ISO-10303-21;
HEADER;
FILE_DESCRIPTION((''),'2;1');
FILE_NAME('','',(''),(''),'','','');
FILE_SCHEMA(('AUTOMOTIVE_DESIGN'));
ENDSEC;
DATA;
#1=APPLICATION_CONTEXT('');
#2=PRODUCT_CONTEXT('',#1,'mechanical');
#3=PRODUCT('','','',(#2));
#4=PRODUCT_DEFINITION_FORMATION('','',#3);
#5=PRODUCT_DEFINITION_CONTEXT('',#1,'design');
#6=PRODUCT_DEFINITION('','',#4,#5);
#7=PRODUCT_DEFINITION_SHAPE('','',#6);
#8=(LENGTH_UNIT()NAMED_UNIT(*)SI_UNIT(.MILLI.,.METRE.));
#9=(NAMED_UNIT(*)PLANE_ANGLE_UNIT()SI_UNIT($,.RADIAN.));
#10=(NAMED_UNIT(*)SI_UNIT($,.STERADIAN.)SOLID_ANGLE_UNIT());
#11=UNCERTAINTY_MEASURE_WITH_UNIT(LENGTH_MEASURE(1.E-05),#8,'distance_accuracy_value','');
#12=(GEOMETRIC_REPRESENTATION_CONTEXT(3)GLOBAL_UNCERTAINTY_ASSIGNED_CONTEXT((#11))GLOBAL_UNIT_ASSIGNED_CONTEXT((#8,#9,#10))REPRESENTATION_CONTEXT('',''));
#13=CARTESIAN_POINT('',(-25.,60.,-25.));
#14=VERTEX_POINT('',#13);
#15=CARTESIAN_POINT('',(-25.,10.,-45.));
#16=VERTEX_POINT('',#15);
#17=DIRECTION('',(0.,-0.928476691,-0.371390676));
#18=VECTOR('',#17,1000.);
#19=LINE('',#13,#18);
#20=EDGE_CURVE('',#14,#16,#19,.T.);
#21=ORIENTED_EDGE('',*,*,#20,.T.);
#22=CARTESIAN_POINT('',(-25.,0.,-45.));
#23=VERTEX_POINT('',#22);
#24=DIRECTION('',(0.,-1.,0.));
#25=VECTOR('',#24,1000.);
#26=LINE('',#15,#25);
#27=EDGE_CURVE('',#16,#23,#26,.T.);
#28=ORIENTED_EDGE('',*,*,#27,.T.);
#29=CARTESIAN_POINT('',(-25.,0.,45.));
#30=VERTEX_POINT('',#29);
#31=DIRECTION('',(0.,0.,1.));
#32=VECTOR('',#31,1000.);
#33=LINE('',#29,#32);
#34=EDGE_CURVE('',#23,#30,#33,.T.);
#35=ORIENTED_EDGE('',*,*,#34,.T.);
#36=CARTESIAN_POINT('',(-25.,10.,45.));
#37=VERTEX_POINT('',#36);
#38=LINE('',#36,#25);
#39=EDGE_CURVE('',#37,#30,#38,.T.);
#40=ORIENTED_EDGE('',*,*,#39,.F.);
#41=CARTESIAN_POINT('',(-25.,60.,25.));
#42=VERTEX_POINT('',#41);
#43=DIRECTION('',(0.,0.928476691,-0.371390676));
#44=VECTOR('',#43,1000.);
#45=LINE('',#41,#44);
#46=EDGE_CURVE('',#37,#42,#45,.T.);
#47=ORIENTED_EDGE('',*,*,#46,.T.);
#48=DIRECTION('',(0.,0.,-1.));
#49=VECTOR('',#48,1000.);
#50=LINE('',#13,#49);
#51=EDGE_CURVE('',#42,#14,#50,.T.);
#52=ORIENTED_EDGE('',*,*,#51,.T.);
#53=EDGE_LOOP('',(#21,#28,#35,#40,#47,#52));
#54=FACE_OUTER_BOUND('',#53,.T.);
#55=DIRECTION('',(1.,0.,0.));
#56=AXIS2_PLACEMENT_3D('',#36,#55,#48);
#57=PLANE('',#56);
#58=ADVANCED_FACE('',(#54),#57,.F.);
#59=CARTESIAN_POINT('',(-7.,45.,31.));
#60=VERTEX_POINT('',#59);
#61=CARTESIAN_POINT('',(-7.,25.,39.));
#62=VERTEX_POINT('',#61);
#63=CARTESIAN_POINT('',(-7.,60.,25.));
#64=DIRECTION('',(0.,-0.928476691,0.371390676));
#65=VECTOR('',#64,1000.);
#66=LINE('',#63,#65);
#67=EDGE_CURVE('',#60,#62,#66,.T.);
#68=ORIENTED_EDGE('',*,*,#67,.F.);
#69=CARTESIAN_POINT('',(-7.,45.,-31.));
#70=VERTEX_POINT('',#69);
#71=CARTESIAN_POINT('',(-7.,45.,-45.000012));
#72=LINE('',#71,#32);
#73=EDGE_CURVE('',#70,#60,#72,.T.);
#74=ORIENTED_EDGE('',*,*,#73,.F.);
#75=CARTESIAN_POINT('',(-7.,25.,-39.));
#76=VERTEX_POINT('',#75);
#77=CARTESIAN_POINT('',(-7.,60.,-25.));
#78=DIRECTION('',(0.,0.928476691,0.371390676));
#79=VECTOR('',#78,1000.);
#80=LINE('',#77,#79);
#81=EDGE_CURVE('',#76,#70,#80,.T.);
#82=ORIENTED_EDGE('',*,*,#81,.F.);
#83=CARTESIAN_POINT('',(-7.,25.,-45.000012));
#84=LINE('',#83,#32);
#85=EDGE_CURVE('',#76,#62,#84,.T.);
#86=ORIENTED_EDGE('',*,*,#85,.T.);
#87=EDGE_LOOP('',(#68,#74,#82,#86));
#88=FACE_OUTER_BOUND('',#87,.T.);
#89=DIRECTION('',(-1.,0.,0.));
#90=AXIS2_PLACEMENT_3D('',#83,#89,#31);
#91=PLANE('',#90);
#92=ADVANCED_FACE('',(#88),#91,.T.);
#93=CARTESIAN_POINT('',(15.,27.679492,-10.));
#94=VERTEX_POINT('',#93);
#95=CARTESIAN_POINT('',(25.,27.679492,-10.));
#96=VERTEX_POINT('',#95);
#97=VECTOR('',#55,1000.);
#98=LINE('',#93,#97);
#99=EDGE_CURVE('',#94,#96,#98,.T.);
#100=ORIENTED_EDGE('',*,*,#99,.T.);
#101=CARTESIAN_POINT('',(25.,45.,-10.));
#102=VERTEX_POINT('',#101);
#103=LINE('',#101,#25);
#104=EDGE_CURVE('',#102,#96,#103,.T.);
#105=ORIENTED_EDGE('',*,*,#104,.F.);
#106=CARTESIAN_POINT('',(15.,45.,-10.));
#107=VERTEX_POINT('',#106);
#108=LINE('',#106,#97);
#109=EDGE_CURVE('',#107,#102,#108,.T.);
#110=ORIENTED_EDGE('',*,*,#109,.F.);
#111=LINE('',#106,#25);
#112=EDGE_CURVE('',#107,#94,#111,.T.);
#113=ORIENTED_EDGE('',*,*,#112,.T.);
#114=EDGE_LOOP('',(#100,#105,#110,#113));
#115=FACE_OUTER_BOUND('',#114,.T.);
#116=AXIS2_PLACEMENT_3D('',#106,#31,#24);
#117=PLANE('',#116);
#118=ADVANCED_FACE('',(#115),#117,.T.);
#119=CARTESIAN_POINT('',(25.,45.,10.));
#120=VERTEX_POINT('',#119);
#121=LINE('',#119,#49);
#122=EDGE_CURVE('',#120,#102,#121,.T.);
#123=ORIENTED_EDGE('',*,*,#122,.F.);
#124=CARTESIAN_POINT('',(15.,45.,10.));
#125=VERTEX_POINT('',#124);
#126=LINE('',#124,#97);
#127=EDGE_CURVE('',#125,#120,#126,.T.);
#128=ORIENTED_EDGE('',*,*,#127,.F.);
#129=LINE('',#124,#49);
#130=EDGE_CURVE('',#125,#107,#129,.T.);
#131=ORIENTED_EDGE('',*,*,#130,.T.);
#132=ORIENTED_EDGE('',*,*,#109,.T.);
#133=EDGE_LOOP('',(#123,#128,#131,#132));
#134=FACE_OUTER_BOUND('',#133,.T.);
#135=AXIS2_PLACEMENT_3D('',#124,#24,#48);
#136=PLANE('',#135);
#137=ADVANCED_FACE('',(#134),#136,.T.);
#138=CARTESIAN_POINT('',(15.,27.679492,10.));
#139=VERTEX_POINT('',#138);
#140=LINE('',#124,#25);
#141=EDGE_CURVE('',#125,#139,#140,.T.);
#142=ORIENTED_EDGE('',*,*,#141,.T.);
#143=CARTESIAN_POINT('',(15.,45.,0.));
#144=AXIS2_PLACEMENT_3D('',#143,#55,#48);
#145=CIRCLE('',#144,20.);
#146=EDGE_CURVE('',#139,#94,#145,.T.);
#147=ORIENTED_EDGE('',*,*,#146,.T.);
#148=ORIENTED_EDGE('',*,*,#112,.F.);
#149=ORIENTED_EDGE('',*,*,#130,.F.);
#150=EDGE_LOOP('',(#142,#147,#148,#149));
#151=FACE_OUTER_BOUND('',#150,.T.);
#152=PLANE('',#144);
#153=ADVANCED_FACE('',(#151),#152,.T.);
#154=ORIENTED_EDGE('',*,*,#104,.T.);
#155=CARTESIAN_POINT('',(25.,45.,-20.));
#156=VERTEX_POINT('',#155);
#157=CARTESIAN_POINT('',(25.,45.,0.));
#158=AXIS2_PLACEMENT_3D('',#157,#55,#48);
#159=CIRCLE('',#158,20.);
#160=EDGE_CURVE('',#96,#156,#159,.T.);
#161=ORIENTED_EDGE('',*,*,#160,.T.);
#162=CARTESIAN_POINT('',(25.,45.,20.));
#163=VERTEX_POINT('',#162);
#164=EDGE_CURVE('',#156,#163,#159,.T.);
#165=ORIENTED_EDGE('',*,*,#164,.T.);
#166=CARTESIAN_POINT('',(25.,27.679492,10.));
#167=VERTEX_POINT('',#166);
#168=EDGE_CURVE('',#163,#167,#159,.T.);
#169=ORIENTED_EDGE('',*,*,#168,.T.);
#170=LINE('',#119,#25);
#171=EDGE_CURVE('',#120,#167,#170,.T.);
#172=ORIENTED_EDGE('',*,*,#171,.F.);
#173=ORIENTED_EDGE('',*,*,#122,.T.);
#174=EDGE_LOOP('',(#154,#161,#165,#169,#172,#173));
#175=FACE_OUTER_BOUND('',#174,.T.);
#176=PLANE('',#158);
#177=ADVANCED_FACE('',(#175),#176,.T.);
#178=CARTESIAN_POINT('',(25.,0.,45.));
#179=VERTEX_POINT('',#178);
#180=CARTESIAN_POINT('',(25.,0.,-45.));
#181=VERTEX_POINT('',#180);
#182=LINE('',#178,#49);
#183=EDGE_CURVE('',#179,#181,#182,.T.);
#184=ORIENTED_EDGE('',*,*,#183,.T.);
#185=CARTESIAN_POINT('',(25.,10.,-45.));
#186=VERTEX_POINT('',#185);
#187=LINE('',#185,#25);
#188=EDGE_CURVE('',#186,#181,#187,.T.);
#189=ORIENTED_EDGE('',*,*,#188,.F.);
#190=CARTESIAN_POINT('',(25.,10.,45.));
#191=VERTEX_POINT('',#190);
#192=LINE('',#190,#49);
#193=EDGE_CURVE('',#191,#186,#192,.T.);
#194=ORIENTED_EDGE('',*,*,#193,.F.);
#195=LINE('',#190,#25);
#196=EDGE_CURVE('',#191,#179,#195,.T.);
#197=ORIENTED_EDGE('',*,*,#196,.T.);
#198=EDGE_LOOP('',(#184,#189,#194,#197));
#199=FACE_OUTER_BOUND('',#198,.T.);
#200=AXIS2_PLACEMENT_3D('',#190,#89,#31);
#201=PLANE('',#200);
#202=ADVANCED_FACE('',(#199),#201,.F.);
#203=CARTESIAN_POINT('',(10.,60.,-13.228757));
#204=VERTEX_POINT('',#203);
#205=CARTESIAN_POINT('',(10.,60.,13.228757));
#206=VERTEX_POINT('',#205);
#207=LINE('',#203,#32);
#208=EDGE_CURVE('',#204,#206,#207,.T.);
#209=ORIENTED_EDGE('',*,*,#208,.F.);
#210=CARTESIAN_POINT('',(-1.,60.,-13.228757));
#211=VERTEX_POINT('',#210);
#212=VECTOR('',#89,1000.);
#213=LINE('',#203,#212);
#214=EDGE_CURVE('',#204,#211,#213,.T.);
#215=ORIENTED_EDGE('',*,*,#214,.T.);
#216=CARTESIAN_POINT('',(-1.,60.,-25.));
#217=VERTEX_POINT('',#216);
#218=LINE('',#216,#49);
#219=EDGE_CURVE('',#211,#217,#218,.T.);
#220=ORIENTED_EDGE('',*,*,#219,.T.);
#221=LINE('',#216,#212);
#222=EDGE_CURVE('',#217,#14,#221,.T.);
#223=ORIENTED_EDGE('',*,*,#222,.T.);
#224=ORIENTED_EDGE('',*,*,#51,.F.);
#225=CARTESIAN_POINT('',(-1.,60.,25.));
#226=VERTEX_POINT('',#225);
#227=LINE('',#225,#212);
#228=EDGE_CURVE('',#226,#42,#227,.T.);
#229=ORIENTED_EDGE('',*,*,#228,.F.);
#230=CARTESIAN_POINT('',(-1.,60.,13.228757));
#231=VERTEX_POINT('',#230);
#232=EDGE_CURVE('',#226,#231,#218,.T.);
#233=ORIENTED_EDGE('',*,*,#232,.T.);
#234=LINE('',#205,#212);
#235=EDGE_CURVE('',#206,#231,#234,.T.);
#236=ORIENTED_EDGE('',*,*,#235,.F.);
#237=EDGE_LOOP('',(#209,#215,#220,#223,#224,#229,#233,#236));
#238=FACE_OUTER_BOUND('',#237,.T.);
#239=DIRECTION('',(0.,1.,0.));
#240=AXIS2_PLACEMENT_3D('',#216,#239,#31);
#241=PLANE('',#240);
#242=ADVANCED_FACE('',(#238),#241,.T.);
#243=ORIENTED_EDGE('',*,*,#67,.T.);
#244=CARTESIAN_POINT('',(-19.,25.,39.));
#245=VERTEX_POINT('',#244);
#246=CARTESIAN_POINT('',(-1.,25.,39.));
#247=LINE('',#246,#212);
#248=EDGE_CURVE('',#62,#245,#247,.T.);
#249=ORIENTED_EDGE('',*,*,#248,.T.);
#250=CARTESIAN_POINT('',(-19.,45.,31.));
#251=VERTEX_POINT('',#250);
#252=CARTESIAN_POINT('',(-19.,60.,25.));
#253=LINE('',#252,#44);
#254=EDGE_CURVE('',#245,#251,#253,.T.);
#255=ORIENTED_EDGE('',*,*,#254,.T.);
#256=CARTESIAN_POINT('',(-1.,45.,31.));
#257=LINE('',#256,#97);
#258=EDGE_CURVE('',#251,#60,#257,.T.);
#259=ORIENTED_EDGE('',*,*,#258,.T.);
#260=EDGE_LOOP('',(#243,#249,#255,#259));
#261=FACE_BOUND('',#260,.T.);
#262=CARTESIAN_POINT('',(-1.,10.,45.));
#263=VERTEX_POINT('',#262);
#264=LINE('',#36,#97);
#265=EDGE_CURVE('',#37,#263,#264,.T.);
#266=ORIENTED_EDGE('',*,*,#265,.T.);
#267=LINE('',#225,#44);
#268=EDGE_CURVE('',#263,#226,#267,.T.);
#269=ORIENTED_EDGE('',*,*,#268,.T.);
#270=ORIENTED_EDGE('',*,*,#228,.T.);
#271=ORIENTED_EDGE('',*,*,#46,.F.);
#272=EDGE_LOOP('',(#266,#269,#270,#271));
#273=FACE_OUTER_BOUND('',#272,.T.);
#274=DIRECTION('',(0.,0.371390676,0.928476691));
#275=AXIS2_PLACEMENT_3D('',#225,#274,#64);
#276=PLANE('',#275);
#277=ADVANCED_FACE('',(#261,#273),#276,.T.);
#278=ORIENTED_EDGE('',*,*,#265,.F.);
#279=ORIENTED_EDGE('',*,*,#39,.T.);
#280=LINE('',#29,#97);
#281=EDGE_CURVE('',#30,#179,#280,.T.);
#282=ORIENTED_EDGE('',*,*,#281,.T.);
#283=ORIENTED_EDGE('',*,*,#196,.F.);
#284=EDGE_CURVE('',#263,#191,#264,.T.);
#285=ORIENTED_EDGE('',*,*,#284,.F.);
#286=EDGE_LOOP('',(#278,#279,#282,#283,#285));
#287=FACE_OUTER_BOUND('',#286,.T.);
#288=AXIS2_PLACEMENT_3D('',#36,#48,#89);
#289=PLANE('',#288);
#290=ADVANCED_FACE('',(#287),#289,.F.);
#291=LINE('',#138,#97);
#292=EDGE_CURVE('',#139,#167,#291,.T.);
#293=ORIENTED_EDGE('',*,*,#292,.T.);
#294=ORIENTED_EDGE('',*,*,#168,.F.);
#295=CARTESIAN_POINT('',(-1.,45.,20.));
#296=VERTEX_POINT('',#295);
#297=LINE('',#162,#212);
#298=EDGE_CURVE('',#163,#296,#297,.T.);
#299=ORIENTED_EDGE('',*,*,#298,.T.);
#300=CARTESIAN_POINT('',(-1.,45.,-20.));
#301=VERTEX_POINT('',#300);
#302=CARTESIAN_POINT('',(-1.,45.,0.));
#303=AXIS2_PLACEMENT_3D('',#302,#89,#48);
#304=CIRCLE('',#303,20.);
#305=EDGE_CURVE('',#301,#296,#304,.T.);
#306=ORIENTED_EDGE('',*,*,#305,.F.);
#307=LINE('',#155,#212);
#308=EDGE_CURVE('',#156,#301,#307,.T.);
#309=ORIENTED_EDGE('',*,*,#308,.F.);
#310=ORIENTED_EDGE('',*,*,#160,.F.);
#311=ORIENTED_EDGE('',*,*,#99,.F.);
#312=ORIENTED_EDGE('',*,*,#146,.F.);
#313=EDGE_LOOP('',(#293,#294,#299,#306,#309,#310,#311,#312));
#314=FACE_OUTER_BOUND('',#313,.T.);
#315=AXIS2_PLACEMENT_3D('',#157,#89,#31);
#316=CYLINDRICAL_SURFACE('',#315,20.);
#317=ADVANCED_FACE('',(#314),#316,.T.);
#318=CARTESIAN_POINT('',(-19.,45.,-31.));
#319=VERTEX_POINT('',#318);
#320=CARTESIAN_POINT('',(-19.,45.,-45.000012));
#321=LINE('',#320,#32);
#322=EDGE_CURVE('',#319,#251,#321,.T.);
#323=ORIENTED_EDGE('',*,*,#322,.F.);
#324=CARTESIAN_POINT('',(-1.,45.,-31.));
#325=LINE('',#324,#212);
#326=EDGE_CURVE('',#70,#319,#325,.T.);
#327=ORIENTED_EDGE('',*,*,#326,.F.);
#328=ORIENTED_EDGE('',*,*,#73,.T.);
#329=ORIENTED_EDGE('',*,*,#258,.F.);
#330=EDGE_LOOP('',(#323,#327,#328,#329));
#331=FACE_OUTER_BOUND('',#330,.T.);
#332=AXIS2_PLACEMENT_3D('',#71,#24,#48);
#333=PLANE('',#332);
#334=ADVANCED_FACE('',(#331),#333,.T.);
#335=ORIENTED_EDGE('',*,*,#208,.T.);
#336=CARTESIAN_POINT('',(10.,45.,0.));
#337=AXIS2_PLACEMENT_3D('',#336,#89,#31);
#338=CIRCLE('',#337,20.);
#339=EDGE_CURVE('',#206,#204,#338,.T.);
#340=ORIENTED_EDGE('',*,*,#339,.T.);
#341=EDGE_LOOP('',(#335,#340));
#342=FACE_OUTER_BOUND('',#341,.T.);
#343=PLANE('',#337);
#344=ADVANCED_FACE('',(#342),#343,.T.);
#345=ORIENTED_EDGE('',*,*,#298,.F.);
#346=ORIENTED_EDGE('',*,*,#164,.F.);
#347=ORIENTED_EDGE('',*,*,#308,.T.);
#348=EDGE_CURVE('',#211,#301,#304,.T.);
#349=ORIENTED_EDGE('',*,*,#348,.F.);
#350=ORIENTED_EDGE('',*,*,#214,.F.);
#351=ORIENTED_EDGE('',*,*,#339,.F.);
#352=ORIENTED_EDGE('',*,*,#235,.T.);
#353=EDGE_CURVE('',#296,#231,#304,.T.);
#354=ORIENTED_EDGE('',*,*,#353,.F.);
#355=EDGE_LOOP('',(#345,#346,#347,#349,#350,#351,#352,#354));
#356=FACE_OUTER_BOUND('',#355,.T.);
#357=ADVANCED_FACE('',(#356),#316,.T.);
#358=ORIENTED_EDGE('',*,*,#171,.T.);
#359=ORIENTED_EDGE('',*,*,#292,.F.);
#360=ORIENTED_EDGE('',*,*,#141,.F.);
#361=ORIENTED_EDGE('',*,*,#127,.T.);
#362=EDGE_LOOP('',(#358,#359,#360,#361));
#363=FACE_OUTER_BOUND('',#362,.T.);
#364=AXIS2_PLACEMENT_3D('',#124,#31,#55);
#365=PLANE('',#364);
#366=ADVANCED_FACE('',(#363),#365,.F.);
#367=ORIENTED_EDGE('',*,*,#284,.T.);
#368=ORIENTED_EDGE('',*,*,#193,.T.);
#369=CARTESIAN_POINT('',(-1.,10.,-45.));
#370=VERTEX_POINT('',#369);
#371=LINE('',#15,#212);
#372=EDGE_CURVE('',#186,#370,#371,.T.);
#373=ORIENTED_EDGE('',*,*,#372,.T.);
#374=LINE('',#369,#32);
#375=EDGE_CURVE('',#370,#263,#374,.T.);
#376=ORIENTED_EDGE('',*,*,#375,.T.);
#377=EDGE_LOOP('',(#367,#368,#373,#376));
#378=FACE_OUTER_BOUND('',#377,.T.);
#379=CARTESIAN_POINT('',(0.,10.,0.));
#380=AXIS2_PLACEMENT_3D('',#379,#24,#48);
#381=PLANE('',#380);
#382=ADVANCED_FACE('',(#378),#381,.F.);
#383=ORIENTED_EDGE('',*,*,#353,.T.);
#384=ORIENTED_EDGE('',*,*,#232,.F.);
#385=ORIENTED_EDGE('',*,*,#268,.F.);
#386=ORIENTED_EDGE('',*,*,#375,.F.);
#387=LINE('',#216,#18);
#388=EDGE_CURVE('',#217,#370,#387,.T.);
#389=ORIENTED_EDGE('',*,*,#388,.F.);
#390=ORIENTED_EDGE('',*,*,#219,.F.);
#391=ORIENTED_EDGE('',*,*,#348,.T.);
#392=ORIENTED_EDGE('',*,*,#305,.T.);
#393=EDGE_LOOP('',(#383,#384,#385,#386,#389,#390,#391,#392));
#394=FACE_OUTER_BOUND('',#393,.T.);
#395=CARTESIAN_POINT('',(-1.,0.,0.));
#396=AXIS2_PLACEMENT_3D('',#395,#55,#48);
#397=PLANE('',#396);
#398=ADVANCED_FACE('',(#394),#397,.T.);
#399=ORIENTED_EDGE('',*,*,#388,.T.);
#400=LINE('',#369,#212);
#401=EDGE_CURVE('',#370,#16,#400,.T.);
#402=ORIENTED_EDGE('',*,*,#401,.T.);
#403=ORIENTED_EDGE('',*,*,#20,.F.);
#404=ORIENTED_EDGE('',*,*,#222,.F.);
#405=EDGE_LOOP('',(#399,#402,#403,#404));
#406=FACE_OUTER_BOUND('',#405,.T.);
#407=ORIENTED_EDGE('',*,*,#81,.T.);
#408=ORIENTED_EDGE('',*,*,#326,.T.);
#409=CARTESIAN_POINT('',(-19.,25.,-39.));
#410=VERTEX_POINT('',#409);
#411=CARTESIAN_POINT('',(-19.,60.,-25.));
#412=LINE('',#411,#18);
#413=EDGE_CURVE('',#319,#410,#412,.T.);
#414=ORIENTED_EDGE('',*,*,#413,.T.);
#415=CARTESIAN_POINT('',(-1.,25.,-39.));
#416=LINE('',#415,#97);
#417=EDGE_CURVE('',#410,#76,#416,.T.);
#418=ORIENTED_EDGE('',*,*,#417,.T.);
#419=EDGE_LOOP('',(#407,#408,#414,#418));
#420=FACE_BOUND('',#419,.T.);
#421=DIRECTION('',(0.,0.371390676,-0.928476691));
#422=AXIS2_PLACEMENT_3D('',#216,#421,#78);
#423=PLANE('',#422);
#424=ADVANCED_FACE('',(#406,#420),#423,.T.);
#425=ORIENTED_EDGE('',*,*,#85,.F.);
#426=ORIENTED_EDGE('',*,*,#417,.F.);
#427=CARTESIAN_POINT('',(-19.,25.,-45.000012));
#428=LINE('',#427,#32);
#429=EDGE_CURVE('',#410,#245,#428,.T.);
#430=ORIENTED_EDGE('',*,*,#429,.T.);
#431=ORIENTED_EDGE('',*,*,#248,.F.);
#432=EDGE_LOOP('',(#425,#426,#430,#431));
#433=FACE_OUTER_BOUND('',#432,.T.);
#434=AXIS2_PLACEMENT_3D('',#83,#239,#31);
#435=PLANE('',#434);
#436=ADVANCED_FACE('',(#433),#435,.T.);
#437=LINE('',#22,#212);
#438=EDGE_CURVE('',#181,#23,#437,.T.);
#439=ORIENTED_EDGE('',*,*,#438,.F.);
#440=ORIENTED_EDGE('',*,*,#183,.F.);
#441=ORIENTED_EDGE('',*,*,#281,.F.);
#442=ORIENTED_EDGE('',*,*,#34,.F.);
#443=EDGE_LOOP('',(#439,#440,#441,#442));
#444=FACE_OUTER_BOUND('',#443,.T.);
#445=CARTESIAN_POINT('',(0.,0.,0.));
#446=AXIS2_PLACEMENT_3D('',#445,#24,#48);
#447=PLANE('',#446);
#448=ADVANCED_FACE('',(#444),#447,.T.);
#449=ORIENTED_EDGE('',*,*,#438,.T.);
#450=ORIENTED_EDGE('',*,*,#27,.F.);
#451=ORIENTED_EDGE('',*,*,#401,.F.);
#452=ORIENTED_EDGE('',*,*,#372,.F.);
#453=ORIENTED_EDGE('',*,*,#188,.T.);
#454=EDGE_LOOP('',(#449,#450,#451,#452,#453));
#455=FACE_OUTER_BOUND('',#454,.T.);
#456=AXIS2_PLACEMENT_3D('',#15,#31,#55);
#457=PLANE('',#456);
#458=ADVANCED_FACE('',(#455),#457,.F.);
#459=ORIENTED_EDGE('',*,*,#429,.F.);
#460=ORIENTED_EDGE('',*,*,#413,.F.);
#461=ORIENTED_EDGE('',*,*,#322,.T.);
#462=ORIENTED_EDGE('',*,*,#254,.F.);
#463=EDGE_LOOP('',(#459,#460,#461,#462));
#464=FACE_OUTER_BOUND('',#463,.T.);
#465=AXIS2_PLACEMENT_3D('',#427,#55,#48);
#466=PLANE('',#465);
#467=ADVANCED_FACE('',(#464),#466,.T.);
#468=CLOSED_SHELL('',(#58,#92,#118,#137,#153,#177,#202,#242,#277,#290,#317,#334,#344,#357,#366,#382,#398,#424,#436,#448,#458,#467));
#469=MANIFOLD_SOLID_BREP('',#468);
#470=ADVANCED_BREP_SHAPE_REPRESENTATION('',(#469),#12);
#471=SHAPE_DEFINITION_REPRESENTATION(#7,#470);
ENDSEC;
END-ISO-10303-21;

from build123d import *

# Parameters (mm, degrees)
BASE_PLATE_SKETCH_W       = 50
BASE_PLATE_SKETCH_H       = 90
BASE_PLATE_90X50X10_DEPTH = 10
UPRIGHT_WEB_DEPTH         = 24
WEB_WINDOW_CUT_DEPTH      = 112.018016556
WEB_WINDOW_CUT_DEPTH_BACK = 100
WEB_WINDOW_SKETCH_W       = 12
WEB_WINDOW_SKETCH_H       = 20
CYLINDER_BOSS_SKETCH_R    = 20
CYLINDER_BOSS_DEPTH       = 26
BOSS_START                = -10
BOSS_END_SLOT_20X10_DEPTH = 10
TOP_NOTCH_CUT_DEPTH       = 11


with BuildPart() as part:
    # Base Plate Sketch → Base Plate 90x50x10 (new body)
    with BuildSketch(Plane(origin=(0, 0, 0), x_dir=(1, 0, 0), z_dir=(0, 1, 0))):
        Rectangle(BASE_PLATE_SKETCH_W, BASE_PLATE_SKETCH_H)
    extrude(amount=BASE_PLATE_90X50X10_DEPTH)

    # Upright Web Sketch → Upright Web (add)
    with BuildSketch(Plane.ZY.offset(25)):
        Polygon((-25, 60), (25, 60), (45, 10), (-45, 10), align=None)
    extrude(amount=-UPRIGHT_WEB_DEPTH)

    # Web Window Sketch → Web Window Cut (cut, two sides: drawn at the far end of the back side and taken through both)
    with BuildSketch(Plane(origin=(0, 0, -45), x_dir=(-1, 0, 0), z_dir=(0, 0, -1)).offset(-WEB_WINDOW_CUT_DEPTH_BACK)):
        with Locations((13, 35)):
            Rectangle(WEB_WINDOW_SKETCH_W, WEB_WINDOW_SKETCH_H)
    extrude(amount=WEB_WINDOW_CUT_DEPTH + WEB_WINDOW_CUT_DEPTH_BACK, mode=Mode.SUBTRACT)

    # Cylinder Boss Sketch → Cylinder Boss (add)
    with BuildSketch(Plane(origin=(-1, 0, 0), x_dir=(0, 0, -1), z_dir=(1, 0, 0))):
        with Locations(Location((0, 45, 0), (0, 0, 131.409622109))):
            Circle(CYLINDER_BOSS_SKETCH_R)
    extrude(amount=CYLINDER_BOSS_DEPTH)

    # Boss End Slot Sketch → Boss End Slot 20x10 (cut)
    with BuildSketch(Plane(origin=(25, 0, 0), x_dir=(0, 0, -1), z_dir=(1, 0, 0)).offset(BOSS_START)):
        with BuildLine():
            Line((-10, 45), (10, 45))
            Line((10, 45), (10, 27.679491924))
            ThreePointArc((10, 27.679491924), (0, 25), (-10, 27.679491924))
            Line((-10, 27.679491924), (-10, 45))
        make_face()
    extrude(amount=BOSS_END_SLOT_20X10_DEPTH, mode=Mode.SUBTRACT)

    # Top Notch Sketch → Top Notch Cut (cut)
    with BuildSketch(Plane.ZY.offset(1)):
        with BuildLine():
            Line((-13.228756555, 60), (13.228756555, 60))
            ThreePointArc((13.228756555, 60), (0, 65), (-13.228756555, 60))
        make_face()
    extrude(amount=-TOP_NOTCH_CUT_DEPTH, mode=Mode.SUBTRACT)


solid = part.part
